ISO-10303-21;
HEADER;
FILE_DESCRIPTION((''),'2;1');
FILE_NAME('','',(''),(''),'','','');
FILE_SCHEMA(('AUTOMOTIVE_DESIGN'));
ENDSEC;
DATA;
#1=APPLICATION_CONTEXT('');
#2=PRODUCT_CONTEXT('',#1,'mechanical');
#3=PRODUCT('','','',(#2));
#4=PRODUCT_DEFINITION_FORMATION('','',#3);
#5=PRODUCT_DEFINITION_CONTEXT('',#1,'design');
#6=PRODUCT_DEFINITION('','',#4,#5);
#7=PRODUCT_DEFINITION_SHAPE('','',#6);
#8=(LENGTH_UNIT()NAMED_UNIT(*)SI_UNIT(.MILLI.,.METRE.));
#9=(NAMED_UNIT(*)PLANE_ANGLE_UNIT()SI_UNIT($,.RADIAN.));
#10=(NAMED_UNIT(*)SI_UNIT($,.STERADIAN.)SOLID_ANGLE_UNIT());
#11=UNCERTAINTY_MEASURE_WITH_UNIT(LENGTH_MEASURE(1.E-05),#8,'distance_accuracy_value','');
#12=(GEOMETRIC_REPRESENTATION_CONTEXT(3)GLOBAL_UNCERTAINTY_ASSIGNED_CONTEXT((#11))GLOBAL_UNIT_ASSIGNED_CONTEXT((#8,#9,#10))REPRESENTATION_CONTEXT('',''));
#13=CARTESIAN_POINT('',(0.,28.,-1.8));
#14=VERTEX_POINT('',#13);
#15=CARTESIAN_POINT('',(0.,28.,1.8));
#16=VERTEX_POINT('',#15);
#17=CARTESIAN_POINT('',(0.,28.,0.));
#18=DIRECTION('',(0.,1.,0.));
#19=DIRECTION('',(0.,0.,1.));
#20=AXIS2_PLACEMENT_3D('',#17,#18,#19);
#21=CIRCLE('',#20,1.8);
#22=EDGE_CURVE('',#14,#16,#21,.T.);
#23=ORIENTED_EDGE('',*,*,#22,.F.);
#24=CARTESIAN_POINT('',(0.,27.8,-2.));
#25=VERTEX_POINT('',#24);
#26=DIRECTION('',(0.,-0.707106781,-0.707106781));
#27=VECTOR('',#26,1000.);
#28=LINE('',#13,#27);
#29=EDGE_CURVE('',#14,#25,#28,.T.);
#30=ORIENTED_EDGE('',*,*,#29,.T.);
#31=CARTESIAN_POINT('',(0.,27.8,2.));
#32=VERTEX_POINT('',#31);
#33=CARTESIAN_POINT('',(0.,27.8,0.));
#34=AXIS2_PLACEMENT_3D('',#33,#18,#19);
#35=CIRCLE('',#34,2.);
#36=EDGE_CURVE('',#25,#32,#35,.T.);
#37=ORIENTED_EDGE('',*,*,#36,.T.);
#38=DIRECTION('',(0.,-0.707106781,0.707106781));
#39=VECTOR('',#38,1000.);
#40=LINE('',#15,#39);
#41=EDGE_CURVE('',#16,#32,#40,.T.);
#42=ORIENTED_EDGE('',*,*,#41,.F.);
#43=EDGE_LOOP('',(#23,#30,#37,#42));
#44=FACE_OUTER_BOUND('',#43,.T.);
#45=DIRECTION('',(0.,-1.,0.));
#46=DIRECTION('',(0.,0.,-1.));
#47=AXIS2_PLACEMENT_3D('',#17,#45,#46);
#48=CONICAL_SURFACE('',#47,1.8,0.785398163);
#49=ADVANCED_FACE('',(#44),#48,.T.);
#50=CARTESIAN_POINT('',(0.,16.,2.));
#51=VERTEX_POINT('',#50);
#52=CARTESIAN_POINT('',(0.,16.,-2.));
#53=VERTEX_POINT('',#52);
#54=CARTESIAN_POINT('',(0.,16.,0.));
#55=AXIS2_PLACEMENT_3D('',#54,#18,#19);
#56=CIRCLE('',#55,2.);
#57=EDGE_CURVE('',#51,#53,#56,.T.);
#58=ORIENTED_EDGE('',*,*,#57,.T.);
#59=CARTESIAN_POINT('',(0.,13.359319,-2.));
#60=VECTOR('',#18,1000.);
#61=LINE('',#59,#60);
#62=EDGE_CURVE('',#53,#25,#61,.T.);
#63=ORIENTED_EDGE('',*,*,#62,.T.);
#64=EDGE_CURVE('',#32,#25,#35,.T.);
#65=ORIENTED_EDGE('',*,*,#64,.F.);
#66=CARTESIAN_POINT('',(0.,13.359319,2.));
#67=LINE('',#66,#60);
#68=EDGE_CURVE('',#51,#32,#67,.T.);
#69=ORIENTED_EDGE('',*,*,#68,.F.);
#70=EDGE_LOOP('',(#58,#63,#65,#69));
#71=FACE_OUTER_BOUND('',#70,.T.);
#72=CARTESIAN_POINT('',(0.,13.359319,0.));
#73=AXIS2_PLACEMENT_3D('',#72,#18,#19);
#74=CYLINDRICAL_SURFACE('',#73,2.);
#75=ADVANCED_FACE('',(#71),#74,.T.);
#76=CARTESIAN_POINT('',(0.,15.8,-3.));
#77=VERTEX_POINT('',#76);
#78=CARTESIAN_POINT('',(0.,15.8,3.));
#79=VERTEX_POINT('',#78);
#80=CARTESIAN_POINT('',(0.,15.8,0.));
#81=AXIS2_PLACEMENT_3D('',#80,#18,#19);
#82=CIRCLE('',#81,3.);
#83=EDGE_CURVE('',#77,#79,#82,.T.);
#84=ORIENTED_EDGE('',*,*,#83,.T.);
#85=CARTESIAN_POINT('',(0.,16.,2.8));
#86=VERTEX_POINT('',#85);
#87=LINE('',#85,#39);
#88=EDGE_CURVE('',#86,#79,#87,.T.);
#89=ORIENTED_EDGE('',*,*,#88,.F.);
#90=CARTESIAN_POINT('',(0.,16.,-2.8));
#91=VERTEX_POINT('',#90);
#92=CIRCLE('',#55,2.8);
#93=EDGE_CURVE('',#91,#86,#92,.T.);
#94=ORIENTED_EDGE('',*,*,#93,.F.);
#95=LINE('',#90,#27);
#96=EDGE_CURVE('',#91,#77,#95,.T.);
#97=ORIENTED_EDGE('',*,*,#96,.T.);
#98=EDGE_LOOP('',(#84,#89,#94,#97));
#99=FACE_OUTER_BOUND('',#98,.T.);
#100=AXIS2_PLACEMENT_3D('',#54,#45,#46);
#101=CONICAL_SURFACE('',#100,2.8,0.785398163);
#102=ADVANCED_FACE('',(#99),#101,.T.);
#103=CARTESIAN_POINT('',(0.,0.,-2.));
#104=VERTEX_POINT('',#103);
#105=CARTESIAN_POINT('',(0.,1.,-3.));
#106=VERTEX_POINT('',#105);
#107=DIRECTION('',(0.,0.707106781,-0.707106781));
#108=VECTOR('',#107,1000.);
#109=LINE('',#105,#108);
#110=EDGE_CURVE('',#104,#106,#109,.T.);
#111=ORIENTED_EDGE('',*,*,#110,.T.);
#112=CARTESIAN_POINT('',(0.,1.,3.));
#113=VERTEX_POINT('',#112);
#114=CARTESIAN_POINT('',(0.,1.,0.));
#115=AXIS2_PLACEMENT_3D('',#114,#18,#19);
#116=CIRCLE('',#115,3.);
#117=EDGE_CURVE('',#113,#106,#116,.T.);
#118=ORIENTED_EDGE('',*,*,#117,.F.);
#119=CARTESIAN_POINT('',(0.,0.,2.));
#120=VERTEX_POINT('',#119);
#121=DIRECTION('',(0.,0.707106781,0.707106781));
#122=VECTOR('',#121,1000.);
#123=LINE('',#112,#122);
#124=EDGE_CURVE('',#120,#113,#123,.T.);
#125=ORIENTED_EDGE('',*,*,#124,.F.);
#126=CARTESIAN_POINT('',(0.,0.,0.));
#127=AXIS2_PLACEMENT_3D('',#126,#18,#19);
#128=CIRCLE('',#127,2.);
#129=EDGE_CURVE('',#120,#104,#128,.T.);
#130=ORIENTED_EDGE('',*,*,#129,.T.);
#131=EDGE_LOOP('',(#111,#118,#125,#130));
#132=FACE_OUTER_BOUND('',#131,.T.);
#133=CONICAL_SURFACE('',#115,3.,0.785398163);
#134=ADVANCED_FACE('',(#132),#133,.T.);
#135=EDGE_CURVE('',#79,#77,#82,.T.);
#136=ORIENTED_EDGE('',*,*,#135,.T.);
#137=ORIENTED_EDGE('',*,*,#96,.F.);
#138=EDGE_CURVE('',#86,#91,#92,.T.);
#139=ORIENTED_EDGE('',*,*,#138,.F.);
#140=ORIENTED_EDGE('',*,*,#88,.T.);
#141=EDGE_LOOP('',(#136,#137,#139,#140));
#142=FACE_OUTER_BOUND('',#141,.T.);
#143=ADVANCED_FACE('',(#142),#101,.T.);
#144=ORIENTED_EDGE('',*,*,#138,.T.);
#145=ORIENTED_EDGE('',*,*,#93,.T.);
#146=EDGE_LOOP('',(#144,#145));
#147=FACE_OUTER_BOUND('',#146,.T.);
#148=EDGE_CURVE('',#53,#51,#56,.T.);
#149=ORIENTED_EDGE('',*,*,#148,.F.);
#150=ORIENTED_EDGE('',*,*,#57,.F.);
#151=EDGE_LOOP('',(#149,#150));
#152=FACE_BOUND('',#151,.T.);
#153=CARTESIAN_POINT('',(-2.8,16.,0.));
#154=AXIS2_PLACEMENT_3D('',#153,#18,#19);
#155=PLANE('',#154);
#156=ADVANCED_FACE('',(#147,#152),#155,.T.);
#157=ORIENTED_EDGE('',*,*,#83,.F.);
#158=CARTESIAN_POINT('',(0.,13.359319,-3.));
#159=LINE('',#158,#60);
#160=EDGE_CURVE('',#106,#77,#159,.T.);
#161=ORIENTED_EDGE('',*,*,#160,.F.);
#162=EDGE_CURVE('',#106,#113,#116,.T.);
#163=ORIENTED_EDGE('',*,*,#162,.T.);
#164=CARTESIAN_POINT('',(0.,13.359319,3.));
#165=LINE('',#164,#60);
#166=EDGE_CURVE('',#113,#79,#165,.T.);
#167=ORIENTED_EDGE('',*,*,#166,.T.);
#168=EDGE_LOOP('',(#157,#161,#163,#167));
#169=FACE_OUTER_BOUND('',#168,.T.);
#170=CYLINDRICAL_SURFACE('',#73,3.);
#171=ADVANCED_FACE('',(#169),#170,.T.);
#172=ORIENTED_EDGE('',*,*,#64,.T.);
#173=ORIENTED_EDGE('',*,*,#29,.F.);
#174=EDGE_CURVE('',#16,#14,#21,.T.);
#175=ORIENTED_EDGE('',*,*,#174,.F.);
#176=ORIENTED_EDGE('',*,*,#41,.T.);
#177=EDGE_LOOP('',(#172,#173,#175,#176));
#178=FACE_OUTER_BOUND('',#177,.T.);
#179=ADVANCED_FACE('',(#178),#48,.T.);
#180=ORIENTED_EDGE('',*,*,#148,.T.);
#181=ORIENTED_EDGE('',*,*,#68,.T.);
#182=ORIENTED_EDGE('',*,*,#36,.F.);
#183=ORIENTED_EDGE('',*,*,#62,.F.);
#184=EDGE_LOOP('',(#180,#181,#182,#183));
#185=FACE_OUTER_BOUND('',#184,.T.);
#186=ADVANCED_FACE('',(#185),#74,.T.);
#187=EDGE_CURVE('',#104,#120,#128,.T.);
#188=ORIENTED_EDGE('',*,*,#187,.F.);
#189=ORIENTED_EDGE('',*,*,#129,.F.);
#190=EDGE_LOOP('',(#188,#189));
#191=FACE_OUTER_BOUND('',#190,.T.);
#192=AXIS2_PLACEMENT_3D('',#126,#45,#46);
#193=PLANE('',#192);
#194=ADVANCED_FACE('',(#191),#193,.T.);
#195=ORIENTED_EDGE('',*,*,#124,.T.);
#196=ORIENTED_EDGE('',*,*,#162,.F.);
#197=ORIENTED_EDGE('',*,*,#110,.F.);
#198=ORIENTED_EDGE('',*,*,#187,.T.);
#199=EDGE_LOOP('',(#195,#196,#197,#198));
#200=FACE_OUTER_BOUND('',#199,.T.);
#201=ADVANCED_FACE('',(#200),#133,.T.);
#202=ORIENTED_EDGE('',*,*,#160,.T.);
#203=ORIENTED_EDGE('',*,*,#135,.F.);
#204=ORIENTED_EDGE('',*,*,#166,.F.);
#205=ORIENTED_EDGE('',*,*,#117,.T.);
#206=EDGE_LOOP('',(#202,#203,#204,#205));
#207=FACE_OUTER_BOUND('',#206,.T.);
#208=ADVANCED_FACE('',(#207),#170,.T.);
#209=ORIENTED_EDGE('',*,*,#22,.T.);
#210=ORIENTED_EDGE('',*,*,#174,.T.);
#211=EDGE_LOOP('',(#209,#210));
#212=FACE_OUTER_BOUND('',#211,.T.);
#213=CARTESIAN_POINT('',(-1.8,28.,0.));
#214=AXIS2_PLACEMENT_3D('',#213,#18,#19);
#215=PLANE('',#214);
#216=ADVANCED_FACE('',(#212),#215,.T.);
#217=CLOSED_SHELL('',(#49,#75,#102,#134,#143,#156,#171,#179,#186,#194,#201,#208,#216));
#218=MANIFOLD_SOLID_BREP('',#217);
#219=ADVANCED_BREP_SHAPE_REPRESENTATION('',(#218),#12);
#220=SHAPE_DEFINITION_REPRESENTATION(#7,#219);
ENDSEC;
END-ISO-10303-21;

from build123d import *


with BuildPart() as part:
    # Sketch1 → Revolve1 (revolve)
    with BuildSketch(Plane.XY, mode=Mode.PRIVATE) as revolve1_sk:
        Polygon((0, 0), (-2, 0), (-3, 1), (-3, 15.8), (-2.8, 16), (-2, 16), (-2, 27.8), (-1.8, 28), (0, 28), align=None)
    revolve(revolve1_sk.sketch.rotate(Axis((0, 13.359319257, 0), (0, -1, 0)), 270), axis=Axis((0, 13.359319257, 0), (0, -1, 0)))


solid = part.part
